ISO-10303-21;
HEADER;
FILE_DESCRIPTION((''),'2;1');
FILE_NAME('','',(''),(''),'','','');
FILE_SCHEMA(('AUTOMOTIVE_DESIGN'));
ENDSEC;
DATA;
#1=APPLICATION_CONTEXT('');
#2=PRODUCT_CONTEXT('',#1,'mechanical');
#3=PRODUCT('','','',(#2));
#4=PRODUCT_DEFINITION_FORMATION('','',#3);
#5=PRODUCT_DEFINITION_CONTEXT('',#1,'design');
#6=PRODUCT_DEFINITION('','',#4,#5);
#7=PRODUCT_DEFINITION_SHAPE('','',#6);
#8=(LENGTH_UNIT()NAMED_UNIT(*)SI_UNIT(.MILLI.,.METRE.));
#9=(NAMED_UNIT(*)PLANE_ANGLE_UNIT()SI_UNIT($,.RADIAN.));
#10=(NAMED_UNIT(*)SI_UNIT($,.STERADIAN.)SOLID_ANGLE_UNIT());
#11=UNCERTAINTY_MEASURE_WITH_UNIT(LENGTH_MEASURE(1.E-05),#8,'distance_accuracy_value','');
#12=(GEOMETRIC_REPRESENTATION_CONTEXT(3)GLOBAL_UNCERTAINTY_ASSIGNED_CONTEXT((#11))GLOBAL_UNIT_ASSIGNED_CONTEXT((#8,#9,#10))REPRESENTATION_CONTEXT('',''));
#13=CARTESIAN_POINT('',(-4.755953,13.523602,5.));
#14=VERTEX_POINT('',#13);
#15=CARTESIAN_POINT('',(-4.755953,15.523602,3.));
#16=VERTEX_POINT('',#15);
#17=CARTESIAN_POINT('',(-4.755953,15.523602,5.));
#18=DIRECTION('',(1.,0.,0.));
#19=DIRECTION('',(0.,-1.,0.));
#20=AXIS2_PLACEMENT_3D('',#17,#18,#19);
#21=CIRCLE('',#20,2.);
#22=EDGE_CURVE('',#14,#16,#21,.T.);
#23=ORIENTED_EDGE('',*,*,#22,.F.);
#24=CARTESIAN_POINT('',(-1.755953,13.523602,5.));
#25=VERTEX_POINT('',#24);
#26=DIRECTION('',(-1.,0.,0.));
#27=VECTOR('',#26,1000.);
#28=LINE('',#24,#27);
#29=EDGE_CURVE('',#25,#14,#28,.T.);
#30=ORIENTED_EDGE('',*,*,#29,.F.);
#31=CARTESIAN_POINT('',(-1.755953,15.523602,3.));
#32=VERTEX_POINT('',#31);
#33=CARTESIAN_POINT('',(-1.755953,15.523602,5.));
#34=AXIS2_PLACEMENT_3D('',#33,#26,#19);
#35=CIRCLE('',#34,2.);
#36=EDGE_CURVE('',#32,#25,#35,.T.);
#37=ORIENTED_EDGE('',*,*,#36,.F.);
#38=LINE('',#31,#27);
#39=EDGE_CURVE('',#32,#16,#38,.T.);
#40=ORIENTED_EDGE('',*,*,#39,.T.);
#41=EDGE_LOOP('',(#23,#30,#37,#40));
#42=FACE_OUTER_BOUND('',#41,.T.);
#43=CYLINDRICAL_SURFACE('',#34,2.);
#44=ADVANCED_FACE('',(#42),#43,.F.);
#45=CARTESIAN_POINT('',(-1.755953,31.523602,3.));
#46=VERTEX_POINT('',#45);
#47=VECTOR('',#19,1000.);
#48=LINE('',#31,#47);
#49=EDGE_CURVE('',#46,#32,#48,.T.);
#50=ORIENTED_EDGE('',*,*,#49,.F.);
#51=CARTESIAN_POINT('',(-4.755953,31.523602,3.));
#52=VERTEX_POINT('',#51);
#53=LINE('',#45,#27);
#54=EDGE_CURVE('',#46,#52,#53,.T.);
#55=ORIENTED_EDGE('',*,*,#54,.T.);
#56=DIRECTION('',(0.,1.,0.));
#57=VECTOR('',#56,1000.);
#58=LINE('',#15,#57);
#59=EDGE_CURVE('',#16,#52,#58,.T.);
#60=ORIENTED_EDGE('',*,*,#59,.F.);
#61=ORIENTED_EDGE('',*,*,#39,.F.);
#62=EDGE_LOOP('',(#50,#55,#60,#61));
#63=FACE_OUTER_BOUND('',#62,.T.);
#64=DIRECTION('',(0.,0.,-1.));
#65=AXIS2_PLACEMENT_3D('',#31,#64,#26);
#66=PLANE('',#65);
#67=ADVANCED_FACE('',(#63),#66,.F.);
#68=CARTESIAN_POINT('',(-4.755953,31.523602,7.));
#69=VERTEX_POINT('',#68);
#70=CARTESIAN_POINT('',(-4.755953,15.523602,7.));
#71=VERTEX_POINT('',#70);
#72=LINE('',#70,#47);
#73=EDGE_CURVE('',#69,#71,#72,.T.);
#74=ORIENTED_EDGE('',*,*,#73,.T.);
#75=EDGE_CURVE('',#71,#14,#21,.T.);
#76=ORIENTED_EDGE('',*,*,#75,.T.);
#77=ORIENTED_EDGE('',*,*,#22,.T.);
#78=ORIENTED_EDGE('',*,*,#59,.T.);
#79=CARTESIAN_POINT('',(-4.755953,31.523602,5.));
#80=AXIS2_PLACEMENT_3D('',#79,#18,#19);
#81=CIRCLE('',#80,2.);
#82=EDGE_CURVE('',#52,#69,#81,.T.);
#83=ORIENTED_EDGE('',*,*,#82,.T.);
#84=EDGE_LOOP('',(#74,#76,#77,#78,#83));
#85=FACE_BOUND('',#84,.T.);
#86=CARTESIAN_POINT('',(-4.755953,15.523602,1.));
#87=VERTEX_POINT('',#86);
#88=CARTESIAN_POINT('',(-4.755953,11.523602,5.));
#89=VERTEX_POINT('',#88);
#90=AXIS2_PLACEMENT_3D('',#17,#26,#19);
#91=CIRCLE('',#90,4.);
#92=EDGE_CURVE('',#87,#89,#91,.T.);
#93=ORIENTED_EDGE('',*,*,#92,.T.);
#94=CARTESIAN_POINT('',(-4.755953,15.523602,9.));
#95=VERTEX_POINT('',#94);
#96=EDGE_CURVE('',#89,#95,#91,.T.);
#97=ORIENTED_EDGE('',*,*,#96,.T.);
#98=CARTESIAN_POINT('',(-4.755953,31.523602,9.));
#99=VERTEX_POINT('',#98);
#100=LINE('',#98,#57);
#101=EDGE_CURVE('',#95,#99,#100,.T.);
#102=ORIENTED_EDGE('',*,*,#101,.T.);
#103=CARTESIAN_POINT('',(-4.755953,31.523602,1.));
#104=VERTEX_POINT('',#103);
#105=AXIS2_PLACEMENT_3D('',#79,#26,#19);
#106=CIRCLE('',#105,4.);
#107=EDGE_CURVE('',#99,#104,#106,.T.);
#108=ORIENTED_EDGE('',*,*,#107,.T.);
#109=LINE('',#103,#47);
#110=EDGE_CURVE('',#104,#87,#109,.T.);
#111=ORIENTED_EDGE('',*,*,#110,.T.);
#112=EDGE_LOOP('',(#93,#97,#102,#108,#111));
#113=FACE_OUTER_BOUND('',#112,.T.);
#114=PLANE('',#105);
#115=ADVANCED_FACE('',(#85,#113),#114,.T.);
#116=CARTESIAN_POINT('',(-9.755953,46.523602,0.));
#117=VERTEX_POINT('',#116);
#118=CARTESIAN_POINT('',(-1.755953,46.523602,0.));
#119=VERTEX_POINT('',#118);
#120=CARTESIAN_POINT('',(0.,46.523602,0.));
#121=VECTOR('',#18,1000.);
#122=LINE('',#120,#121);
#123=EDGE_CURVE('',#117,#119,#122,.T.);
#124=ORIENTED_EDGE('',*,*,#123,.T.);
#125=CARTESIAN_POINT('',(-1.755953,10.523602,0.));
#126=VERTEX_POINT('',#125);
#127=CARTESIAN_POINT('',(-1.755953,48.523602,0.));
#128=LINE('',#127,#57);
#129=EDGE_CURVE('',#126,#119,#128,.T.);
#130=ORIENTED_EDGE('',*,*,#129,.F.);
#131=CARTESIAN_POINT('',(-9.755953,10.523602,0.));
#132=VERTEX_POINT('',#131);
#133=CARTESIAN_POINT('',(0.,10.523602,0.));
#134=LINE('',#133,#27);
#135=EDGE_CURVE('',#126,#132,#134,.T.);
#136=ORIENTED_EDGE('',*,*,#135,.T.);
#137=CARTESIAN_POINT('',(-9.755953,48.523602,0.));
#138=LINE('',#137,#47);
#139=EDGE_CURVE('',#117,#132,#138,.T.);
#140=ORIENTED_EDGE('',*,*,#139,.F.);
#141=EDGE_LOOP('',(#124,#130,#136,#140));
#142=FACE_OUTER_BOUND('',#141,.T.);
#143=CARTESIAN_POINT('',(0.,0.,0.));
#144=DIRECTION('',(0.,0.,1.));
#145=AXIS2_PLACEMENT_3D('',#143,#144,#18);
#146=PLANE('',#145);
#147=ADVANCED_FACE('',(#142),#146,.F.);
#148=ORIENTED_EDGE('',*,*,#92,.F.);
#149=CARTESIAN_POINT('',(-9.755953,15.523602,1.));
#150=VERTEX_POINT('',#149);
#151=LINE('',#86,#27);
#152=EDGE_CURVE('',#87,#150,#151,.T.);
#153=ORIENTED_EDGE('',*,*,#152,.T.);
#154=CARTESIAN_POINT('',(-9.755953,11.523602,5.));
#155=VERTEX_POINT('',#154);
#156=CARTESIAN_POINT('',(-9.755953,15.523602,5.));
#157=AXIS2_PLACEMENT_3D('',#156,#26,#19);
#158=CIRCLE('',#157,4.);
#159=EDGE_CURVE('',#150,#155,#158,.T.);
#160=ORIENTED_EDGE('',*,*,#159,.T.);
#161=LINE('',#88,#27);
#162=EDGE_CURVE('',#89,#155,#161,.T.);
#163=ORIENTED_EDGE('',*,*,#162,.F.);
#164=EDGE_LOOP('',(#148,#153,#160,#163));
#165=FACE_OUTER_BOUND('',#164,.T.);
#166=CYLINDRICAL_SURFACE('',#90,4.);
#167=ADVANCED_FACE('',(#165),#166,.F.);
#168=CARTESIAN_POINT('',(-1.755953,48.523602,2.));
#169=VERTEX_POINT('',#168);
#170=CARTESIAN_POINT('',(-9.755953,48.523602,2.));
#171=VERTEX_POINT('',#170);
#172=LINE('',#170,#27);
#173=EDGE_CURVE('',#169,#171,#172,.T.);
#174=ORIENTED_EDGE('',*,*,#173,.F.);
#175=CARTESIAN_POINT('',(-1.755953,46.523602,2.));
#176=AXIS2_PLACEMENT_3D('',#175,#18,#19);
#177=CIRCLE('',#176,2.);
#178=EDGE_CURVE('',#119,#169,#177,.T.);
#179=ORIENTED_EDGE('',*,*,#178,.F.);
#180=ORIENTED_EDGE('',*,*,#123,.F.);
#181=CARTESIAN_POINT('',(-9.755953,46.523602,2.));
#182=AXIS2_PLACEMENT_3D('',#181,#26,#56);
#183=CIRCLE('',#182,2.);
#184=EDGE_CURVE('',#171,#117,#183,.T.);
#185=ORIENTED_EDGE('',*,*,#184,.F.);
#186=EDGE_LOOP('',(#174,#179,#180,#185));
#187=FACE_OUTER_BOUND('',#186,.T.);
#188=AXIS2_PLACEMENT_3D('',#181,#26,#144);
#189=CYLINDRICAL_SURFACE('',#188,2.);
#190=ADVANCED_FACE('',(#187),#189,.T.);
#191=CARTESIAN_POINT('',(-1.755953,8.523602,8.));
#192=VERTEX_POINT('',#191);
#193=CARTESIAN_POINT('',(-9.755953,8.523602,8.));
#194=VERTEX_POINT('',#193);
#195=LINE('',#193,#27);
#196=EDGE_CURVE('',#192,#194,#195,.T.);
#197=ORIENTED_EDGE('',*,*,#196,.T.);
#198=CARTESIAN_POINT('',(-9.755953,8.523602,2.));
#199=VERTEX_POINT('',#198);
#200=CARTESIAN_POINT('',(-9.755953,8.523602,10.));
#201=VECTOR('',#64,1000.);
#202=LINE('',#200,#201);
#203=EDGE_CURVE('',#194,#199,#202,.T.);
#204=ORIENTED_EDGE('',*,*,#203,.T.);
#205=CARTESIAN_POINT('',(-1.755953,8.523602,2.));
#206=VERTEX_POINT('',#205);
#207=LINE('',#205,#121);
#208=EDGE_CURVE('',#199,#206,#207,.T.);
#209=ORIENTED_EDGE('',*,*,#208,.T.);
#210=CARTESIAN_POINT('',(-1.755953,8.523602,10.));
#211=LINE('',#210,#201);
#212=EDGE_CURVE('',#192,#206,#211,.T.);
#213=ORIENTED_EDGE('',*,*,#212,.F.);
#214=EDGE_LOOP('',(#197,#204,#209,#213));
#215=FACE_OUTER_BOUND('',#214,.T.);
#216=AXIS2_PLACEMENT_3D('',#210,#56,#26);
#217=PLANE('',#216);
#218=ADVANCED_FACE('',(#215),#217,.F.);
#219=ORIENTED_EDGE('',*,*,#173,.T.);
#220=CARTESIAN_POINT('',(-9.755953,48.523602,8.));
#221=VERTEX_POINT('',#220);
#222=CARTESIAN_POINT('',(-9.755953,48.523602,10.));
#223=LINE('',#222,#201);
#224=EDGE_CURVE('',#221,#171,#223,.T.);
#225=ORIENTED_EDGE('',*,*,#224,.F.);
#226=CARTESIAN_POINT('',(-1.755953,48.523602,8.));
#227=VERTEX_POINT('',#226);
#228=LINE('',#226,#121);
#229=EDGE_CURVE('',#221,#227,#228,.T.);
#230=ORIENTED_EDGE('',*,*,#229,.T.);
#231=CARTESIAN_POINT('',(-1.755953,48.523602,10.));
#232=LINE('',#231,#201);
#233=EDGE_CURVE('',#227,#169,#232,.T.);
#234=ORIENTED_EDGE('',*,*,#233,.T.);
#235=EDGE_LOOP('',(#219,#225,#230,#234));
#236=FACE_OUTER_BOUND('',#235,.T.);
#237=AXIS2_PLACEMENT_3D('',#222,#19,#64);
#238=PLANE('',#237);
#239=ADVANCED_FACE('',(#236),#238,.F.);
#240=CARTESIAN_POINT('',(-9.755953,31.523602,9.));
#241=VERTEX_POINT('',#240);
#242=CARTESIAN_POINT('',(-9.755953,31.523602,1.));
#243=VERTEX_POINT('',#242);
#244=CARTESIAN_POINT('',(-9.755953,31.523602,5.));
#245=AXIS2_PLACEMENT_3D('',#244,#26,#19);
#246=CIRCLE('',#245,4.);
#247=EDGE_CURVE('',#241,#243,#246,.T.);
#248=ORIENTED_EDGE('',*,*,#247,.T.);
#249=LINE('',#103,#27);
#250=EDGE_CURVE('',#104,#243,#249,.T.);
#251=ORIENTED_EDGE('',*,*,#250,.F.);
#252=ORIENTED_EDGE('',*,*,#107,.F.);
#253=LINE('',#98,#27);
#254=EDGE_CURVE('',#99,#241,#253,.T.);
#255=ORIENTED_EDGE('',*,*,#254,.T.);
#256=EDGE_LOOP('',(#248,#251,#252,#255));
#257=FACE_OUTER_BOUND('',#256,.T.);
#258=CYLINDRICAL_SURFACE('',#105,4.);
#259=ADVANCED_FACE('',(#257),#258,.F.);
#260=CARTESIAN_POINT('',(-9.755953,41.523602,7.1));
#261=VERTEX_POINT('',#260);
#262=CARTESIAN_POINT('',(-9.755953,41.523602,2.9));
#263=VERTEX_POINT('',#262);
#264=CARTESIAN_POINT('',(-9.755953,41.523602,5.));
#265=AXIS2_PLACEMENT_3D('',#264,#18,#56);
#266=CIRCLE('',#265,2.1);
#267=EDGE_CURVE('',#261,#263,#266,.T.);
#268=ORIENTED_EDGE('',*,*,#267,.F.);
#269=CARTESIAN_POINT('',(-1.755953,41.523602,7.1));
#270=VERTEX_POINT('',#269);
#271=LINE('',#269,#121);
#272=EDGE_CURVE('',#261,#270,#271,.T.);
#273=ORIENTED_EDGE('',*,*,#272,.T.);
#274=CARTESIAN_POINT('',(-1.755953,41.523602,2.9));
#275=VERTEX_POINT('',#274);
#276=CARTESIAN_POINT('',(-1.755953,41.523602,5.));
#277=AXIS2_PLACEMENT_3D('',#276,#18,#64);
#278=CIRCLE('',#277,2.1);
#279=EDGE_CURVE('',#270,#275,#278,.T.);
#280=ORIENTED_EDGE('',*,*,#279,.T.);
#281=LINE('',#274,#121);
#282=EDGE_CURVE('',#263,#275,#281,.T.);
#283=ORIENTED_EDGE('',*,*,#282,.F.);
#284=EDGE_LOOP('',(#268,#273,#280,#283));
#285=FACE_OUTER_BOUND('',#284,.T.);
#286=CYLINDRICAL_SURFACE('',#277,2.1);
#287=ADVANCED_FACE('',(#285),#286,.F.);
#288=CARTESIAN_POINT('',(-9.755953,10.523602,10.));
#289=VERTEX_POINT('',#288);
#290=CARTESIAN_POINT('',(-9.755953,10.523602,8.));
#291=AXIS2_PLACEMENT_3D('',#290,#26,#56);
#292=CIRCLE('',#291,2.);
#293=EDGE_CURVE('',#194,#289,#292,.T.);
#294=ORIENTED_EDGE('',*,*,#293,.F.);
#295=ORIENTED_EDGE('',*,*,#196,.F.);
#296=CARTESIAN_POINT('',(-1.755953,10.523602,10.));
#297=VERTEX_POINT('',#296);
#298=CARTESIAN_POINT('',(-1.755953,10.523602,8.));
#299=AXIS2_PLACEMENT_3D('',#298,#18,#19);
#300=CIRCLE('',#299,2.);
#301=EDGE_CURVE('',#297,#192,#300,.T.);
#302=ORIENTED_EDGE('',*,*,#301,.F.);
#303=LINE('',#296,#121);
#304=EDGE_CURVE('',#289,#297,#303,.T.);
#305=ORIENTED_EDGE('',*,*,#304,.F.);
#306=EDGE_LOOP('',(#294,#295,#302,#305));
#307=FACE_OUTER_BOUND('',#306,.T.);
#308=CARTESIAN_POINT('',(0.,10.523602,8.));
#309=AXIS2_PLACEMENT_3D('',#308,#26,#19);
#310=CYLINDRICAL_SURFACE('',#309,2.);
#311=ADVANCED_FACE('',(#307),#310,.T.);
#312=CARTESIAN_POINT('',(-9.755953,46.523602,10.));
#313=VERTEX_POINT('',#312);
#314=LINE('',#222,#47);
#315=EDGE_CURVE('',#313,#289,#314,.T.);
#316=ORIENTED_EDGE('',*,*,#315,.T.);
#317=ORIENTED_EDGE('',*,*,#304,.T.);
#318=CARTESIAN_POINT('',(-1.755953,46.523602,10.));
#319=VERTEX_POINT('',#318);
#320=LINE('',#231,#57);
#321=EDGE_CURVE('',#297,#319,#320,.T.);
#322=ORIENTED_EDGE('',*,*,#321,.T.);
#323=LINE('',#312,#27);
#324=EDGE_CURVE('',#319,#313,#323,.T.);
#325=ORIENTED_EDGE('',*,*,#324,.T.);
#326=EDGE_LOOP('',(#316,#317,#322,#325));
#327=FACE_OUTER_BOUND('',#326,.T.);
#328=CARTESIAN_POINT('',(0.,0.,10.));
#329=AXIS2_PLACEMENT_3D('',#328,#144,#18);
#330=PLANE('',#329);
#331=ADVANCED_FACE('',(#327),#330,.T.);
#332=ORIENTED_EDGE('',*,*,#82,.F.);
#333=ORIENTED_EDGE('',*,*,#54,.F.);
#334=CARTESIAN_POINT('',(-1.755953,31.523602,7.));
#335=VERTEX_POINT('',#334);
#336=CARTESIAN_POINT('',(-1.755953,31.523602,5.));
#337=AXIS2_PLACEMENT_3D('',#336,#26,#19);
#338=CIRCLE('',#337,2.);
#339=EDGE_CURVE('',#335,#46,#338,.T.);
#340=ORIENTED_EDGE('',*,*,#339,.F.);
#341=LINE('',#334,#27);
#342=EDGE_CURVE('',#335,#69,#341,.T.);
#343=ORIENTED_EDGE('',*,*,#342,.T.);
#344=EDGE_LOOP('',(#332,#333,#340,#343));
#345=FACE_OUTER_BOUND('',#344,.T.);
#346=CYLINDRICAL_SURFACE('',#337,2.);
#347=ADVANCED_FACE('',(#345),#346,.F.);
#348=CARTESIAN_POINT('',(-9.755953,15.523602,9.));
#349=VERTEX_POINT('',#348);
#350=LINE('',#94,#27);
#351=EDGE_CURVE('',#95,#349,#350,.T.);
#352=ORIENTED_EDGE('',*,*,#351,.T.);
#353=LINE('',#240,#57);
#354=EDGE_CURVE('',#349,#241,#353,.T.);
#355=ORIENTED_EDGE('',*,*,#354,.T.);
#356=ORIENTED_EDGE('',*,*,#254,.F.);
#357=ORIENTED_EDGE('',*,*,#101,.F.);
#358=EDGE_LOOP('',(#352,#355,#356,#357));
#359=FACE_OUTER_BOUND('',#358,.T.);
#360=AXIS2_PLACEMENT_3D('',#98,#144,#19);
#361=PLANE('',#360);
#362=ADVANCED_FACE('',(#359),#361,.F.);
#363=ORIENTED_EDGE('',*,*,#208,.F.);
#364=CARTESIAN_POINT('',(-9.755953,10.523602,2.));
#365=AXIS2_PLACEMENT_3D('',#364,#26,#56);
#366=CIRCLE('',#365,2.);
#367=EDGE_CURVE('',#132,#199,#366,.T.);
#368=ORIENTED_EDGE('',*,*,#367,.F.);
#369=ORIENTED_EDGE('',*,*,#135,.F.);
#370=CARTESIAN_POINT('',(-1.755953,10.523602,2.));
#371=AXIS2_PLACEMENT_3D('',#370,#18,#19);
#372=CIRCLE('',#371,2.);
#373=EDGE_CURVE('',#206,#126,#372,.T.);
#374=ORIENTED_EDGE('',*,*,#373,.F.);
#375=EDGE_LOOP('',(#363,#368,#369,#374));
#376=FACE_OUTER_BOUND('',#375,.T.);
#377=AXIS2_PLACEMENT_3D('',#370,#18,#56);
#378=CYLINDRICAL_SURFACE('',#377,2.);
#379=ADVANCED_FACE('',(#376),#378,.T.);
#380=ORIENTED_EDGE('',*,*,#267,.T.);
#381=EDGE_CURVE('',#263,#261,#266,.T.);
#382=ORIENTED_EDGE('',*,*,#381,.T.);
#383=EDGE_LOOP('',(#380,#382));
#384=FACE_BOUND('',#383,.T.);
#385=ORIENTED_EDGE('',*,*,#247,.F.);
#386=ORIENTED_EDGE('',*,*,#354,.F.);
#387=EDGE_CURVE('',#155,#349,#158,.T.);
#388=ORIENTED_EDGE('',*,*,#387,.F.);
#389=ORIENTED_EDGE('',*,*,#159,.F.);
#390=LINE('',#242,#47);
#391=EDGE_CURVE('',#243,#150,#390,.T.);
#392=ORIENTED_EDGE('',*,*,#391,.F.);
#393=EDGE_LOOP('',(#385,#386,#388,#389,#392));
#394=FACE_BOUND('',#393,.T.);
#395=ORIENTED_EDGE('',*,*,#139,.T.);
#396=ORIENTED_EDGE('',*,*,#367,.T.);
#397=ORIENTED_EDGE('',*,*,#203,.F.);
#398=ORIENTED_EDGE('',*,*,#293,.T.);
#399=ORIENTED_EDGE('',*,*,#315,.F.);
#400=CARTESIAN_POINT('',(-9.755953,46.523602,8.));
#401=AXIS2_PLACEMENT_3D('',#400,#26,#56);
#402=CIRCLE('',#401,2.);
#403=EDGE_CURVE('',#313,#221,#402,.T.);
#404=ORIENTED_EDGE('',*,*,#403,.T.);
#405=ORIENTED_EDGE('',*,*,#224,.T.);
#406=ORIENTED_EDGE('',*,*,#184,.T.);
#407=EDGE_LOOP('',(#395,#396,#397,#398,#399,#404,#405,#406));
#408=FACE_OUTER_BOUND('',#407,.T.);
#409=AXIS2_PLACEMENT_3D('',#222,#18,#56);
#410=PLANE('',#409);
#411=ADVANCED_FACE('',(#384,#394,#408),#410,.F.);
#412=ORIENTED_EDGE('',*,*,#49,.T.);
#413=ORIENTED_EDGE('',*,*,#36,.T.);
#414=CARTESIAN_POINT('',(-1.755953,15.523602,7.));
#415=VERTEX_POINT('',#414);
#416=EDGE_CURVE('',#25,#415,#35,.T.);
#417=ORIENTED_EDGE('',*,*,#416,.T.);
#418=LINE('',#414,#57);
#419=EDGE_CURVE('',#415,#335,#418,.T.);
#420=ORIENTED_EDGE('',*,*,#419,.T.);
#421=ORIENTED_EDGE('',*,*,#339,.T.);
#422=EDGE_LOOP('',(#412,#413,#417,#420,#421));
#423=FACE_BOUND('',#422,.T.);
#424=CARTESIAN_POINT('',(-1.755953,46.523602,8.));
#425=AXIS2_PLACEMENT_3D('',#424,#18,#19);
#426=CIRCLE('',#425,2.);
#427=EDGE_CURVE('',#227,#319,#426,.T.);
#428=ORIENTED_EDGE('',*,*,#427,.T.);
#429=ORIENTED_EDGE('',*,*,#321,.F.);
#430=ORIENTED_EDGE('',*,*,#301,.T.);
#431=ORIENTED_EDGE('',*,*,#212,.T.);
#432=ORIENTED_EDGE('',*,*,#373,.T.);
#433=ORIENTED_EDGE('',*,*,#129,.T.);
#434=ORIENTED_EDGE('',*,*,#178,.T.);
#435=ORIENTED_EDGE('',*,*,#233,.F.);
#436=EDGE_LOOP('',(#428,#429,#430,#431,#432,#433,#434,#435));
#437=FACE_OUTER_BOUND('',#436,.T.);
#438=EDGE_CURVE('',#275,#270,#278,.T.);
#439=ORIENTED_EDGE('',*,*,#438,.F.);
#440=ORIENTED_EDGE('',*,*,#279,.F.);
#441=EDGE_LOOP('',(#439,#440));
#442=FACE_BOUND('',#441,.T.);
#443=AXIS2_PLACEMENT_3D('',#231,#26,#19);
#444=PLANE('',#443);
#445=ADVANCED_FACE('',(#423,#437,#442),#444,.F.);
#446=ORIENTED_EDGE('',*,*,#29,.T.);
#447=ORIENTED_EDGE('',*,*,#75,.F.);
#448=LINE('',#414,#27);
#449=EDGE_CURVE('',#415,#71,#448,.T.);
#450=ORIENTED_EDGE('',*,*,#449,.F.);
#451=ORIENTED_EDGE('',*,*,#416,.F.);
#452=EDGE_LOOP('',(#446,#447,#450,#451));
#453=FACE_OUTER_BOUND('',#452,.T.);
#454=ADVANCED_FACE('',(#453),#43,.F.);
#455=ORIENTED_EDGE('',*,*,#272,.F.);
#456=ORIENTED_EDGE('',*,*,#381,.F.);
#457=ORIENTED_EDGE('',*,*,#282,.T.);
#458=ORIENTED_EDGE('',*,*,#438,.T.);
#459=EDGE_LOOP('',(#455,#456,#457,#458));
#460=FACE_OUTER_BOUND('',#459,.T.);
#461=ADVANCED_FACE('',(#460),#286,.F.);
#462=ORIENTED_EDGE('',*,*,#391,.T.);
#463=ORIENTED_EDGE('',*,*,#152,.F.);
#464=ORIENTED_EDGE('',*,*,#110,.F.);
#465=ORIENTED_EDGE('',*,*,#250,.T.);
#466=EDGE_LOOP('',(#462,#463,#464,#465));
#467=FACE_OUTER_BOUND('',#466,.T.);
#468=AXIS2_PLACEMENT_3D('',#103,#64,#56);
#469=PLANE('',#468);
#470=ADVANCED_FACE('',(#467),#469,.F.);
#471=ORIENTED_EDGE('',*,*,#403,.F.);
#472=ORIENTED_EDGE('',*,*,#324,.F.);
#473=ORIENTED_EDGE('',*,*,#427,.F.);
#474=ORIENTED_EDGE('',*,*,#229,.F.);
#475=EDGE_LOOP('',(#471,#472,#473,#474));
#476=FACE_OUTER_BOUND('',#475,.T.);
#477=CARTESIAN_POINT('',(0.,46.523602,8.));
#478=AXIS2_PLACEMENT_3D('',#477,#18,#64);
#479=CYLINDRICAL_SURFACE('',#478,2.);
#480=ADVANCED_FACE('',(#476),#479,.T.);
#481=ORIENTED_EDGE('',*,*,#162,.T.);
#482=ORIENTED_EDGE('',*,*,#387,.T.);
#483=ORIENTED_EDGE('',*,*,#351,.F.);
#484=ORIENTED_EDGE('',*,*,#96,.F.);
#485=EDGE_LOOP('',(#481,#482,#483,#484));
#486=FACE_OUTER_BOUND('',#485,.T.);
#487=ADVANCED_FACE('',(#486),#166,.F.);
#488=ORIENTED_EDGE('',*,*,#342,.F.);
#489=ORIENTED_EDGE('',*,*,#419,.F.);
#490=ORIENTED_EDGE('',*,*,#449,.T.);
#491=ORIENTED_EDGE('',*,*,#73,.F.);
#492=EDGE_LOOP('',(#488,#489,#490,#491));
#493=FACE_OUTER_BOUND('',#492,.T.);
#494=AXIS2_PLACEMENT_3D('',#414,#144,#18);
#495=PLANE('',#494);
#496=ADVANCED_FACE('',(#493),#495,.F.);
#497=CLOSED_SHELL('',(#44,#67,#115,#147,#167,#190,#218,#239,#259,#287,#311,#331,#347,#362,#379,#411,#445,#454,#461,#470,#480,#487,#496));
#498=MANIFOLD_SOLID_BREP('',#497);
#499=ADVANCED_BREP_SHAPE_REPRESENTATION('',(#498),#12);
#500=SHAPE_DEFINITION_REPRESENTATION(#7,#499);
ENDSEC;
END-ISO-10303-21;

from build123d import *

# Parameters (mm, degrees)
SKETCH_1_W             = 8
SKETCH_1_H             = 40
EXTRUDE_1_DEPTH        = 10
HOLE_WIZARD_M5_1_D     = 4.2
HOLE_WIZARD_M5_1_DEPTH = 12.4
HOLE_WIZARD_M5_1_TIP   = 1.2618073
FILLET_1_R             = 2
CUT_EXTRUDE_1_DEPTH    = 51.185056966
CUT_EXTRUDE_2_DEPTH    = 5
FILLET_2_R             = 2


with BuildPart() as part:
    # 草图1 → 凸台-拉伸1 (new body)
    with BuildSketch(Plane.XY):
        with Locations((-5.75595287, 28.523601913)):
            Rectangle(SKETCH_1_W, SKETCH_1_H)
    extrude(amount=EXTRUDE_1_DEPTH)

    # M5 螺纹孔1
    with Locations(Plane(origin=(-1.75595287, 0, 0), x_dir=(0, 0, -1), z_dir=(1, 0, 0))):
        with Locations((-5, 41.523601913)):
            Hole(HOLE_WIZARD_M5_1_D / 2, depth=HOLE_WIZARD_M5_1_DEPTH)
            with Locations((0, 0, -(HOLE_WIZARD_M5_1_DEPTH + HOLE_WIZARD_M5_1_TIP / 2))):  # 118° drill point
                Cone(0, HOLE_WIZARD_M5_1_D / 2, HOLE_WIZARD_M5_1_TIP, mode=Mode.SUBTRACT)

    # 圆角1
    fillet_1_edges = [part.edges().sort_by_distance(p)[0] for p in [
        (-5.75595287, 48.523601913, 10),
        (-5.75595287, 48.523601913, 0),
    ]]
    fillet(fillet_1_edges, radius=FILLET_1_R)

    # 草图5 → 切除-拉伸1 (cut, through all)
    with BuildSketch(Plane.ZY.offset(9.75595287)):
        with BuildLine():
            Line((3, 15.523601913), (3, 31.523601913))
            ThreePointArc((3, 31.523601913), (5, 33.523601913), (7, 31.523601913))
            Line((7, 31.523601913), (7, 15.523601913))
            ThreePointArc((7, 15.523601913), (5, 13.523601913), (3, 15.523601913))
        make_face()
    extrude(amount=-CUT_EXTRUDE_1_DEPTH, mode=Mode.SUBTRACT)

    # 草图6 → 切除-拉伸2 (cut)
    with BuildSketch(Plane.ZY.offset(9.75595287)):
        with BuildLine():
            Line((9, 31.523601913), (9, 15.523601913))
            ThreePointArc((9, 15.523601913), (5, 11.523601913), (1, 15.523601913))
            Line((1, 15.523601913), (1, 31.523601913))
            ThreePointArc((1, 31.523601913), (5, 35.523601913), (9, 31.523601913))
        make_face()
    extrude(amount=-CUT_EXTRUDE_2_DEPTH, mode=Mode.SUBTRACT)

    # 圆角2
    fillet_2_edges = [part.edges().sort_by_distance(p)[0] for p in [
        (-5.75595287, 8.523601913, 10),
        (-5.75595287, 8.523601913, 0),
    ]]
    fillet(fillet_2_edges, radius=FILLET_2_R)


solid = part.part
